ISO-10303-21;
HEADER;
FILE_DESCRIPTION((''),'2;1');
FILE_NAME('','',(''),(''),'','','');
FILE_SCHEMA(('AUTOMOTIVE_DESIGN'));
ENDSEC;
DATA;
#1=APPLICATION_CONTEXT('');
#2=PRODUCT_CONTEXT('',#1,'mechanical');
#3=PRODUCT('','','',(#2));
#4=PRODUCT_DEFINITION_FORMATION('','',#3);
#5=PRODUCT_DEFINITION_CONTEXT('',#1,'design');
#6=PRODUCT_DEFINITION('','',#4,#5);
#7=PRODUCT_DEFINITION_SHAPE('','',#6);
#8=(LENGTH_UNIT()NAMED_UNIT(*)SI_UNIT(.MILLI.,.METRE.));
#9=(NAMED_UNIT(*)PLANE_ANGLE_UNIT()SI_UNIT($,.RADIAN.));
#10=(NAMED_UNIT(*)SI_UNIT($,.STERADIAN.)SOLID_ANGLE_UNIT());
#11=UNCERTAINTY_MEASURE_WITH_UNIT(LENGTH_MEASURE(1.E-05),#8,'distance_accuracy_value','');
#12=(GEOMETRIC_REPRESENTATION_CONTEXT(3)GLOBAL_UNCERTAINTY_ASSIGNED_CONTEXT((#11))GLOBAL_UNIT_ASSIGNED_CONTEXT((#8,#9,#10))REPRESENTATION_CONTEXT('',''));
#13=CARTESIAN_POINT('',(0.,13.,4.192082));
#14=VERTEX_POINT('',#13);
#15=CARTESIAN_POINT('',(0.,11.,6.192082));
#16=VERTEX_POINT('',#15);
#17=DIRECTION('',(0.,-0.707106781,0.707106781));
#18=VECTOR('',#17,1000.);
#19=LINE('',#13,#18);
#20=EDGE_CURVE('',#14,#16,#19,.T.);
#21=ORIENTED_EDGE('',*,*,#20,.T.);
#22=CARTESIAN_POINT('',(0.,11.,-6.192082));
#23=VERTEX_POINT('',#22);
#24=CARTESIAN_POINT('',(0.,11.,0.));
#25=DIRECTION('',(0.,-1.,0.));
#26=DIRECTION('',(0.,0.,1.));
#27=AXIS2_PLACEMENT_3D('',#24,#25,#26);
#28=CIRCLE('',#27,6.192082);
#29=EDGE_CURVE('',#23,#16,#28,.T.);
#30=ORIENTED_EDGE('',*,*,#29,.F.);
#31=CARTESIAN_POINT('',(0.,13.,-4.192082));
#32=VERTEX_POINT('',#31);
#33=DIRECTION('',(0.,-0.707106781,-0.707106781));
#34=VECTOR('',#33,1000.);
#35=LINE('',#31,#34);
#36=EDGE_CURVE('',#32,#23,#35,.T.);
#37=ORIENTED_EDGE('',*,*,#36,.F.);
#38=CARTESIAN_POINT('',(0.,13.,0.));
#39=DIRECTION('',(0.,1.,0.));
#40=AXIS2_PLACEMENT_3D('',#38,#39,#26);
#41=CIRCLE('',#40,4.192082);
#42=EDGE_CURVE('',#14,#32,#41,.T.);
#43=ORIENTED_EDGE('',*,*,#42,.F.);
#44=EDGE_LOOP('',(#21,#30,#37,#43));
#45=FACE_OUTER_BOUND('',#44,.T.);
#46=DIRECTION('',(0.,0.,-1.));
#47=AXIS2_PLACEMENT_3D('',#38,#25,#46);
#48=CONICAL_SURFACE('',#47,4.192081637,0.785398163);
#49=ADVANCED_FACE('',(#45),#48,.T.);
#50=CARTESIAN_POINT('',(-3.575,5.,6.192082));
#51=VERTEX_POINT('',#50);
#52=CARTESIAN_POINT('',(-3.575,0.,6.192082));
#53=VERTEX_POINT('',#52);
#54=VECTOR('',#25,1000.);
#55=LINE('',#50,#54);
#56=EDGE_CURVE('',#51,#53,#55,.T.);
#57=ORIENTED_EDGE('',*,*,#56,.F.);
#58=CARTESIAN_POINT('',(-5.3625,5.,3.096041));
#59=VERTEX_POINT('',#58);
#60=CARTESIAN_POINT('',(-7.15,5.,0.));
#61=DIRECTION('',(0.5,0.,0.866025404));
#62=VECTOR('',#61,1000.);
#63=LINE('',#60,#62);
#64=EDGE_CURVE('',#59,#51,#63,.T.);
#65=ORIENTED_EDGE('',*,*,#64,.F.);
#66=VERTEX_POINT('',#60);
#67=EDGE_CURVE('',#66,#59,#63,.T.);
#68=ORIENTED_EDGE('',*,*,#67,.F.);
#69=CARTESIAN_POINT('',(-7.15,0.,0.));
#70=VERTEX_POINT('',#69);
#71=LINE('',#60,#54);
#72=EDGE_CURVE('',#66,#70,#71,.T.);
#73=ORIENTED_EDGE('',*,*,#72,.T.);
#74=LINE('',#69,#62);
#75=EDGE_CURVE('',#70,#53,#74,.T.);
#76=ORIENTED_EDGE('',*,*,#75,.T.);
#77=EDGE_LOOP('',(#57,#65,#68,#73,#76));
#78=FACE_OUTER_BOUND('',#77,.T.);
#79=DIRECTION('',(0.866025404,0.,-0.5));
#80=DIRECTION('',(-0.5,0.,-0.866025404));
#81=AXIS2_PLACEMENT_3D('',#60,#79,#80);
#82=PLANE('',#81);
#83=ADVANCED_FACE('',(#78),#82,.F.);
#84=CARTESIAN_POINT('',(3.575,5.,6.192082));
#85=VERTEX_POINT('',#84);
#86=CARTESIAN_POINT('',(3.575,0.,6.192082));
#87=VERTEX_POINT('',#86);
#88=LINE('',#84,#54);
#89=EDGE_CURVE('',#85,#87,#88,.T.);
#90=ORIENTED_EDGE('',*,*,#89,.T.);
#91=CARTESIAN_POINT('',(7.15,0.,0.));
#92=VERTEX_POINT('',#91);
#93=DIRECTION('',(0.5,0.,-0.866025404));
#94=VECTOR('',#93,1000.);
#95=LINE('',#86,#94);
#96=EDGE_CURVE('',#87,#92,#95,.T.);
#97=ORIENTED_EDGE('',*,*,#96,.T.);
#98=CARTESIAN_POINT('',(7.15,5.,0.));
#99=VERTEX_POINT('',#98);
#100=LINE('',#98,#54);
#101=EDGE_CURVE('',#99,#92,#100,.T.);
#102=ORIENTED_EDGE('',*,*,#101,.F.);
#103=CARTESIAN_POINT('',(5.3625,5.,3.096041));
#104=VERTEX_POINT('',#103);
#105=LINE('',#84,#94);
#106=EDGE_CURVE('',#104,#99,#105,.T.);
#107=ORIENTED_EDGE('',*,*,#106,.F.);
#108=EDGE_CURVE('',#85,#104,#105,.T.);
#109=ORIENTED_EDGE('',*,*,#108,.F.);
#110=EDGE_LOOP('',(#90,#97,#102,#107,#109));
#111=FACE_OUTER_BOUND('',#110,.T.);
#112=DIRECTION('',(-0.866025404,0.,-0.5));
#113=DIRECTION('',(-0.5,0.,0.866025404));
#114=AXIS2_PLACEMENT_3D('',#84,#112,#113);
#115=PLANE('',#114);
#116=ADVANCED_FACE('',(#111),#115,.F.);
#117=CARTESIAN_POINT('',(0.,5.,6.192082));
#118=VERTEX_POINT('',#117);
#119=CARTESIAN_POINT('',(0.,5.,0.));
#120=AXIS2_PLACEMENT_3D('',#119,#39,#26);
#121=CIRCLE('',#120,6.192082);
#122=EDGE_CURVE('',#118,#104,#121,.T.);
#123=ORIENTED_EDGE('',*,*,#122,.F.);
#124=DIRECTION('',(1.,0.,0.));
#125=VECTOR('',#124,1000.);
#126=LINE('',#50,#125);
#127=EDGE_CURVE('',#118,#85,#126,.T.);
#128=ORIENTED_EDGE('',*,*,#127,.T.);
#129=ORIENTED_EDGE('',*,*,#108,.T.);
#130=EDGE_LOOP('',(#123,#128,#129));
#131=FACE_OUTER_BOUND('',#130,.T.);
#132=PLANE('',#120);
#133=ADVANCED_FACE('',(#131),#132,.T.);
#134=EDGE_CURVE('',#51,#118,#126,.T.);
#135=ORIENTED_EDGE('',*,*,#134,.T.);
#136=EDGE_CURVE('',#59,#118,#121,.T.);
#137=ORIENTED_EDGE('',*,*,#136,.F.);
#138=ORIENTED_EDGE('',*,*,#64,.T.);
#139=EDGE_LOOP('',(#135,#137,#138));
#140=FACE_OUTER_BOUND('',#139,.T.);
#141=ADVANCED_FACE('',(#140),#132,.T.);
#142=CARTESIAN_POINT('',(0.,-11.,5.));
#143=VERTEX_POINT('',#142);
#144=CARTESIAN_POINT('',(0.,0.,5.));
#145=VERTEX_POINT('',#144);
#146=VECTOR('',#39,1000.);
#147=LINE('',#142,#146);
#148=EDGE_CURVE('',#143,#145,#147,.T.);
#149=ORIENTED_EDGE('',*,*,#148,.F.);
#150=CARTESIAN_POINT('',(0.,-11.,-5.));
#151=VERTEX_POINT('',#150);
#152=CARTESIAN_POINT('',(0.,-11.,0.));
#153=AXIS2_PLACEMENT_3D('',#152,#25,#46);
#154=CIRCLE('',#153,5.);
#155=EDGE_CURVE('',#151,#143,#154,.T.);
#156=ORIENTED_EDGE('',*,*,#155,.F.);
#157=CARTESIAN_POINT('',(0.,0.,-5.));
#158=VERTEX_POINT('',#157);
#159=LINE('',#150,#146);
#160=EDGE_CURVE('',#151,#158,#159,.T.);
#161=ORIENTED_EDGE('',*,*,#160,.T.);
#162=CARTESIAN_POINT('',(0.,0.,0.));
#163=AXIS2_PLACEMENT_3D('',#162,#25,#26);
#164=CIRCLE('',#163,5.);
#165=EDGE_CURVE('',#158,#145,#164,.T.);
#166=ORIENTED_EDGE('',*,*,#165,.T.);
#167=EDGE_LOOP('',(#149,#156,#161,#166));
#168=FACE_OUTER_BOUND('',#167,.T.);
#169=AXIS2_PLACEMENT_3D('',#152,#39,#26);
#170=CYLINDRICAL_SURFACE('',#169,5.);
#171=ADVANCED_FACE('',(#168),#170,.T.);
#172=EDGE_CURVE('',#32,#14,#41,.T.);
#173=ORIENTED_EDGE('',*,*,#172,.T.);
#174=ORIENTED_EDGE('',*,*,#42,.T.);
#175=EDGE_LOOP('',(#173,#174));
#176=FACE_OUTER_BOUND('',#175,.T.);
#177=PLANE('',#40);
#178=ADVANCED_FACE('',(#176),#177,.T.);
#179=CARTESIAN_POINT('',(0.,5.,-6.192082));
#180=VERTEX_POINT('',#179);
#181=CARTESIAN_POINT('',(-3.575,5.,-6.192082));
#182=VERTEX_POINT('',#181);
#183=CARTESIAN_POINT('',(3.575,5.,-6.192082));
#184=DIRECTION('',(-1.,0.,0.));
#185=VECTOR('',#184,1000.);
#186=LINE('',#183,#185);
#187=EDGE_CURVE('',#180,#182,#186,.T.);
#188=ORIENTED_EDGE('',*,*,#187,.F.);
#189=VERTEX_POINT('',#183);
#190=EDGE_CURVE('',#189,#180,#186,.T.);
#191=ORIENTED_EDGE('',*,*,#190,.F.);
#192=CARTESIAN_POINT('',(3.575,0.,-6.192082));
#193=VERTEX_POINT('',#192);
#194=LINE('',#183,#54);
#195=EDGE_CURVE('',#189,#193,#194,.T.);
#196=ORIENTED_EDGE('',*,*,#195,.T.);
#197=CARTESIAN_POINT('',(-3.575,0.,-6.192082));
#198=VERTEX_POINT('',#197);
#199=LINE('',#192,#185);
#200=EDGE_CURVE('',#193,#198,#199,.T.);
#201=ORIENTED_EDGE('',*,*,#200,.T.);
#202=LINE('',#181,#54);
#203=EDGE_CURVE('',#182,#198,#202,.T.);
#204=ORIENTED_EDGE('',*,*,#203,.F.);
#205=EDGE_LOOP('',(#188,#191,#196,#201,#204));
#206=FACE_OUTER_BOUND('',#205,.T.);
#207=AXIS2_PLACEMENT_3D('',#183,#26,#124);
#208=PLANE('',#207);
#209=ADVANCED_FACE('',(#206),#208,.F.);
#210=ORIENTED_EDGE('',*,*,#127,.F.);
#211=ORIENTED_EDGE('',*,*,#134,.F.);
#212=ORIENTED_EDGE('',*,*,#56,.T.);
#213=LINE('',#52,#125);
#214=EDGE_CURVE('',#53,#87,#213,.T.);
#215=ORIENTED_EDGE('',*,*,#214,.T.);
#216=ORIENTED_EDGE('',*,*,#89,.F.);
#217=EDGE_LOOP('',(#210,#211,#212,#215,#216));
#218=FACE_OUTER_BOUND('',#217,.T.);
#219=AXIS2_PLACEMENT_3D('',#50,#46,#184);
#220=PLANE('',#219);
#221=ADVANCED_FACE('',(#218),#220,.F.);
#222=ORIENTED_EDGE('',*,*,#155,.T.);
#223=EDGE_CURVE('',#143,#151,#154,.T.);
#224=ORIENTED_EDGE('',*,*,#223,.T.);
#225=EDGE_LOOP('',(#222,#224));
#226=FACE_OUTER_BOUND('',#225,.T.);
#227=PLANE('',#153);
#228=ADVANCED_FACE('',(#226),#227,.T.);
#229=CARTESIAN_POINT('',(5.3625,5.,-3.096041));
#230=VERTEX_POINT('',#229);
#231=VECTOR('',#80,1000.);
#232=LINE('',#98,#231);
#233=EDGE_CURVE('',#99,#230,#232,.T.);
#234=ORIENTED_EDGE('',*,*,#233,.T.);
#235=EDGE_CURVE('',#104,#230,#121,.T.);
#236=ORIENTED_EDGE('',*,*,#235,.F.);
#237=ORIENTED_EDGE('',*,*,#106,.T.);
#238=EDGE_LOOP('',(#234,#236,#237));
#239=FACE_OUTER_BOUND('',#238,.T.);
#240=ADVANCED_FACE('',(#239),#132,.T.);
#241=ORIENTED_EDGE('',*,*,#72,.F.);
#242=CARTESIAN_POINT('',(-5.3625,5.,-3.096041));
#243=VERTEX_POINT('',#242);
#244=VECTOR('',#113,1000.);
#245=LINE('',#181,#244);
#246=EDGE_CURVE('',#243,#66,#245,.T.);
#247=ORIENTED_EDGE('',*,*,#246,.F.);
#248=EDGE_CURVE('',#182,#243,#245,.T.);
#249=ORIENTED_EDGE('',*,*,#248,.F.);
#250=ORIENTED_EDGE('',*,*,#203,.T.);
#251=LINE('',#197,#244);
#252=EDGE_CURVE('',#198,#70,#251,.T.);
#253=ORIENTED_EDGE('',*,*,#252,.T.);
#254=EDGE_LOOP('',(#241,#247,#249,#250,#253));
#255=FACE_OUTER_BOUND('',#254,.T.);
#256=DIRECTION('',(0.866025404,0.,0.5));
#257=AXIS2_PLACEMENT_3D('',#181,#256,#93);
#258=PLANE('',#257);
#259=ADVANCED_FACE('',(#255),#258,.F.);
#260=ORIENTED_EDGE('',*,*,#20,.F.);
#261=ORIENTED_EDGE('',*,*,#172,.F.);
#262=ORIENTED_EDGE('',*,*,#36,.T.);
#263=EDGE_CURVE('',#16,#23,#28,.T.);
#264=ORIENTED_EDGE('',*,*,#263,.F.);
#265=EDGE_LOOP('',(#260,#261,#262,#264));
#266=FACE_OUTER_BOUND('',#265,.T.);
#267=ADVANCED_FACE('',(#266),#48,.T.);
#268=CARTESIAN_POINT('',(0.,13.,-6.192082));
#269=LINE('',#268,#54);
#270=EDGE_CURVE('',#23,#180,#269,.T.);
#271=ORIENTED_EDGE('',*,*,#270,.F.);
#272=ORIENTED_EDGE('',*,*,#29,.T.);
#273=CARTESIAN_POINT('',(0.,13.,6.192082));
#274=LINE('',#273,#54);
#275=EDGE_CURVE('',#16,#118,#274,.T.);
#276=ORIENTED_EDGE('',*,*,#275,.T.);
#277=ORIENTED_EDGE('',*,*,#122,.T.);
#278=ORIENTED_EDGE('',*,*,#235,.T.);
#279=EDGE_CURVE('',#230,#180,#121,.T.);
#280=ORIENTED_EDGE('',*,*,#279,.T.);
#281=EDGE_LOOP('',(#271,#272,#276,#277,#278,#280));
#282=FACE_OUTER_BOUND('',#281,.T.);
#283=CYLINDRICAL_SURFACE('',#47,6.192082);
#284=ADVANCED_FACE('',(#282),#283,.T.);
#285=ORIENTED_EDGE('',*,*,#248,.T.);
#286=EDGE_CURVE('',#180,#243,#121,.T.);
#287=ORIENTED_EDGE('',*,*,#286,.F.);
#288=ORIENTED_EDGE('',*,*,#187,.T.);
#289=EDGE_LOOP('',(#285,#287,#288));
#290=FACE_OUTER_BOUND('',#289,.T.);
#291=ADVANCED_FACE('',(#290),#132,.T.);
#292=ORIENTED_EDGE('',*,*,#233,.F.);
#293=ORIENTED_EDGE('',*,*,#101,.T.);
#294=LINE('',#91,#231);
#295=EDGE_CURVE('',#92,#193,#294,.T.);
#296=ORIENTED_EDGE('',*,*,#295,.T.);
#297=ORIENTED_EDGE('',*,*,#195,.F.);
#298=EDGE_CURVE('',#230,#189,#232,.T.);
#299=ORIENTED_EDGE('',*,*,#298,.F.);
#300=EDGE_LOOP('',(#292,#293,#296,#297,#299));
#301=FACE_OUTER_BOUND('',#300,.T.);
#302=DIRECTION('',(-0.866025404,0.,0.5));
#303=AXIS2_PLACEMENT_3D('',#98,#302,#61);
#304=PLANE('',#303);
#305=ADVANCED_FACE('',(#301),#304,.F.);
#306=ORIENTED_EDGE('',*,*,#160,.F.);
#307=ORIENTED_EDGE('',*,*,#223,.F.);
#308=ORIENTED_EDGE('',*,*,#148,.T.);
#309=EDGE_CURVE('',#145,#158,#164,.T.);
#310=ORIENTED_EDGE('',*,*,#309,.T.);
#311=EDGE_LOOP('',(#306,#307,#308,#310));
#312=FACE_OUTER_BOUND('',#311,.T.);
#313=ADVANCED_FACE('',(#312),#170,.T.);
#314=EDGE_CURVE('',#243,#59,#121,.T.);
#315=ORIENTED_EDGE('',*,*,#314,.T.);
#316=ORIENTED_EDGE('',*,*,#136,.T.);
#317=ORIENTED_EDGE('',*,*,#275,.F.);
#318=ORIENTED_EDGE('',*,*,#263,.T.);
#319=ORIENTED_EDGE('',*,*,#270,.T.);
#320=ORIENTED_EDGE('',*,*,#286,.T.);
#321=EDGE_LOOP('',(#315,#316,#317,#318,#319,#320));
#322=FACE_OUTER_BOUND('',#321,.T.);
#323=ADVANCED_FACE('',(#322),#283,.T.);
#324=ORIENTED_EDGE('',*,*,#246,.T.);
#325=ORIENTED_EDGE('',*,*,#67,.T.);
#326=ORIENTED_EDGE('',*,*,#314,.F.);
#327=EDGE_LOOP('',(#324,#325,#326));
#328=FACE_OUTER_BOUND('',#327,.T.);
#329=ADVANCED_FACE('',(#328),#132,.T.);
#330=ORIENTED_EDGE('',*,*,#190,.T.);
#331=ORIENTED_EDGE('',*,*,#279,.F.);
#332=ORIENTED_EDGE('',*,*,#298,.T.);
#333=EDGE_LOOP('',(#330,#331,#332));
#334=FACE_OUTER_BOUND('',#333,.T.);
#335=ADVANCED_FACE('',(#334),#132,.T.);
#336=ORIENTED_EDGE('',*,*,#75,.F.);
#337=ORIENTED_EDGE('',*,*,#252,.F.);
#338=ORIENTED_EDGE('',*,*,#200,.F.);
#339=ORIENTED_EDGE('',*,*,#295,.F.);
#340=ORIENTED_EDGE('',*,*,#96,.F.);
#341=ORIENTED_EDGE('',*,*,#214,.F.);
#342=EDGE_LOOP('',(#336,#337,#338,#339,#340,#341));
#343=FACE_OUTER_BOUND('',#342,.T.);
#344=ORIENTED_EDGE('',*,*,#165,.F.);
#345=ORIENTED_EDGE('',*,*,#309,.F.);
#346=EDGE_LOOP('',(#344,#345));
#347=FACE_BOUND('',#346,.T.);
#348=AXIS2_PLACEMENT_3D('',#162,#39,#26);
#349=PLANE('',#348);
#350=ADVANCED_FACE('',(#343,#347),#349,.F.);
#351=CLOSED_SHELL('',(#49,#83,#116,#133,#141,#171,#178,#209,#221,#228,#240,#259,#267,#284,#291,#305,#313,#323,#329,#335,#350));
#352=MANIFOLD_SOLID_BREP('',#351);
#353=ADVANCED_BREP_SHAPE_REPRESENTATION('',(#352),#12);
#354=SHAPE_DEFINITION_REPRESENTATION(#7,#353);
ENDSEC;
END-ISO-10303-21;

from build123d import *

# Parameters (mm, degrees)
EXTRUDE_1_DEPTH = 5
SKETCH_2_R      = 6.192081637
EXTRUDE_2_DEPTH = 8
CHAMFER_1_SIZE  = 2
SKETCH_3_R      = 5
EXTRUDE_3_DEPTH = 11


with BuildPart() as part:
    # 草图1 → 凸台-拉伸1 (new body)
    with BuildSketch(Plane(origin=(0, 0, 0), x_dir=(1, 0, 0), z_dir=(0, 1, 0))):
        Polygon((-7.15, 0), (-3.575, -6.192081637), (3.575, -6.192081637), (7.15, 0), (3.575, 6.192081637), (-3.575, 6.192081637), align=None)
    extrude(amount=EXTRUDE_1_DEPTH)

    # 草图2 → 凸台-拉伸2 (add)
    with BuildSketch(Plane(origin=(0, 5, 0), x_dir=(1, 0, 0), z_dir=(0, 1, 0))):
        with Locations(Location((0, 0, 0), (0, 0, 270))):
            Circle(SKETCH_2_R)
    extrude(amount=EXTRUDE_2_DEPTH)

    # 倒角1
    chamfer_1_edges = [part.edges().sort_by_distance(p)[0] for p in [
        (0, 13, -6.192081637),
    ]]
    chamfer(chamfer_1_edges, length=CHAMFER_1_SIZE)

    # 草图3 → 凸台-拉伸3 (add)
    with BuildSketch(Plane.XZ):
        with Locations(Location((0, 0, 0), (0, 0, 90))):
            Circle(SKETCH_3_R)
    extrude(amount=EXTRUDE_3_DEPTH)


solid = part.part
